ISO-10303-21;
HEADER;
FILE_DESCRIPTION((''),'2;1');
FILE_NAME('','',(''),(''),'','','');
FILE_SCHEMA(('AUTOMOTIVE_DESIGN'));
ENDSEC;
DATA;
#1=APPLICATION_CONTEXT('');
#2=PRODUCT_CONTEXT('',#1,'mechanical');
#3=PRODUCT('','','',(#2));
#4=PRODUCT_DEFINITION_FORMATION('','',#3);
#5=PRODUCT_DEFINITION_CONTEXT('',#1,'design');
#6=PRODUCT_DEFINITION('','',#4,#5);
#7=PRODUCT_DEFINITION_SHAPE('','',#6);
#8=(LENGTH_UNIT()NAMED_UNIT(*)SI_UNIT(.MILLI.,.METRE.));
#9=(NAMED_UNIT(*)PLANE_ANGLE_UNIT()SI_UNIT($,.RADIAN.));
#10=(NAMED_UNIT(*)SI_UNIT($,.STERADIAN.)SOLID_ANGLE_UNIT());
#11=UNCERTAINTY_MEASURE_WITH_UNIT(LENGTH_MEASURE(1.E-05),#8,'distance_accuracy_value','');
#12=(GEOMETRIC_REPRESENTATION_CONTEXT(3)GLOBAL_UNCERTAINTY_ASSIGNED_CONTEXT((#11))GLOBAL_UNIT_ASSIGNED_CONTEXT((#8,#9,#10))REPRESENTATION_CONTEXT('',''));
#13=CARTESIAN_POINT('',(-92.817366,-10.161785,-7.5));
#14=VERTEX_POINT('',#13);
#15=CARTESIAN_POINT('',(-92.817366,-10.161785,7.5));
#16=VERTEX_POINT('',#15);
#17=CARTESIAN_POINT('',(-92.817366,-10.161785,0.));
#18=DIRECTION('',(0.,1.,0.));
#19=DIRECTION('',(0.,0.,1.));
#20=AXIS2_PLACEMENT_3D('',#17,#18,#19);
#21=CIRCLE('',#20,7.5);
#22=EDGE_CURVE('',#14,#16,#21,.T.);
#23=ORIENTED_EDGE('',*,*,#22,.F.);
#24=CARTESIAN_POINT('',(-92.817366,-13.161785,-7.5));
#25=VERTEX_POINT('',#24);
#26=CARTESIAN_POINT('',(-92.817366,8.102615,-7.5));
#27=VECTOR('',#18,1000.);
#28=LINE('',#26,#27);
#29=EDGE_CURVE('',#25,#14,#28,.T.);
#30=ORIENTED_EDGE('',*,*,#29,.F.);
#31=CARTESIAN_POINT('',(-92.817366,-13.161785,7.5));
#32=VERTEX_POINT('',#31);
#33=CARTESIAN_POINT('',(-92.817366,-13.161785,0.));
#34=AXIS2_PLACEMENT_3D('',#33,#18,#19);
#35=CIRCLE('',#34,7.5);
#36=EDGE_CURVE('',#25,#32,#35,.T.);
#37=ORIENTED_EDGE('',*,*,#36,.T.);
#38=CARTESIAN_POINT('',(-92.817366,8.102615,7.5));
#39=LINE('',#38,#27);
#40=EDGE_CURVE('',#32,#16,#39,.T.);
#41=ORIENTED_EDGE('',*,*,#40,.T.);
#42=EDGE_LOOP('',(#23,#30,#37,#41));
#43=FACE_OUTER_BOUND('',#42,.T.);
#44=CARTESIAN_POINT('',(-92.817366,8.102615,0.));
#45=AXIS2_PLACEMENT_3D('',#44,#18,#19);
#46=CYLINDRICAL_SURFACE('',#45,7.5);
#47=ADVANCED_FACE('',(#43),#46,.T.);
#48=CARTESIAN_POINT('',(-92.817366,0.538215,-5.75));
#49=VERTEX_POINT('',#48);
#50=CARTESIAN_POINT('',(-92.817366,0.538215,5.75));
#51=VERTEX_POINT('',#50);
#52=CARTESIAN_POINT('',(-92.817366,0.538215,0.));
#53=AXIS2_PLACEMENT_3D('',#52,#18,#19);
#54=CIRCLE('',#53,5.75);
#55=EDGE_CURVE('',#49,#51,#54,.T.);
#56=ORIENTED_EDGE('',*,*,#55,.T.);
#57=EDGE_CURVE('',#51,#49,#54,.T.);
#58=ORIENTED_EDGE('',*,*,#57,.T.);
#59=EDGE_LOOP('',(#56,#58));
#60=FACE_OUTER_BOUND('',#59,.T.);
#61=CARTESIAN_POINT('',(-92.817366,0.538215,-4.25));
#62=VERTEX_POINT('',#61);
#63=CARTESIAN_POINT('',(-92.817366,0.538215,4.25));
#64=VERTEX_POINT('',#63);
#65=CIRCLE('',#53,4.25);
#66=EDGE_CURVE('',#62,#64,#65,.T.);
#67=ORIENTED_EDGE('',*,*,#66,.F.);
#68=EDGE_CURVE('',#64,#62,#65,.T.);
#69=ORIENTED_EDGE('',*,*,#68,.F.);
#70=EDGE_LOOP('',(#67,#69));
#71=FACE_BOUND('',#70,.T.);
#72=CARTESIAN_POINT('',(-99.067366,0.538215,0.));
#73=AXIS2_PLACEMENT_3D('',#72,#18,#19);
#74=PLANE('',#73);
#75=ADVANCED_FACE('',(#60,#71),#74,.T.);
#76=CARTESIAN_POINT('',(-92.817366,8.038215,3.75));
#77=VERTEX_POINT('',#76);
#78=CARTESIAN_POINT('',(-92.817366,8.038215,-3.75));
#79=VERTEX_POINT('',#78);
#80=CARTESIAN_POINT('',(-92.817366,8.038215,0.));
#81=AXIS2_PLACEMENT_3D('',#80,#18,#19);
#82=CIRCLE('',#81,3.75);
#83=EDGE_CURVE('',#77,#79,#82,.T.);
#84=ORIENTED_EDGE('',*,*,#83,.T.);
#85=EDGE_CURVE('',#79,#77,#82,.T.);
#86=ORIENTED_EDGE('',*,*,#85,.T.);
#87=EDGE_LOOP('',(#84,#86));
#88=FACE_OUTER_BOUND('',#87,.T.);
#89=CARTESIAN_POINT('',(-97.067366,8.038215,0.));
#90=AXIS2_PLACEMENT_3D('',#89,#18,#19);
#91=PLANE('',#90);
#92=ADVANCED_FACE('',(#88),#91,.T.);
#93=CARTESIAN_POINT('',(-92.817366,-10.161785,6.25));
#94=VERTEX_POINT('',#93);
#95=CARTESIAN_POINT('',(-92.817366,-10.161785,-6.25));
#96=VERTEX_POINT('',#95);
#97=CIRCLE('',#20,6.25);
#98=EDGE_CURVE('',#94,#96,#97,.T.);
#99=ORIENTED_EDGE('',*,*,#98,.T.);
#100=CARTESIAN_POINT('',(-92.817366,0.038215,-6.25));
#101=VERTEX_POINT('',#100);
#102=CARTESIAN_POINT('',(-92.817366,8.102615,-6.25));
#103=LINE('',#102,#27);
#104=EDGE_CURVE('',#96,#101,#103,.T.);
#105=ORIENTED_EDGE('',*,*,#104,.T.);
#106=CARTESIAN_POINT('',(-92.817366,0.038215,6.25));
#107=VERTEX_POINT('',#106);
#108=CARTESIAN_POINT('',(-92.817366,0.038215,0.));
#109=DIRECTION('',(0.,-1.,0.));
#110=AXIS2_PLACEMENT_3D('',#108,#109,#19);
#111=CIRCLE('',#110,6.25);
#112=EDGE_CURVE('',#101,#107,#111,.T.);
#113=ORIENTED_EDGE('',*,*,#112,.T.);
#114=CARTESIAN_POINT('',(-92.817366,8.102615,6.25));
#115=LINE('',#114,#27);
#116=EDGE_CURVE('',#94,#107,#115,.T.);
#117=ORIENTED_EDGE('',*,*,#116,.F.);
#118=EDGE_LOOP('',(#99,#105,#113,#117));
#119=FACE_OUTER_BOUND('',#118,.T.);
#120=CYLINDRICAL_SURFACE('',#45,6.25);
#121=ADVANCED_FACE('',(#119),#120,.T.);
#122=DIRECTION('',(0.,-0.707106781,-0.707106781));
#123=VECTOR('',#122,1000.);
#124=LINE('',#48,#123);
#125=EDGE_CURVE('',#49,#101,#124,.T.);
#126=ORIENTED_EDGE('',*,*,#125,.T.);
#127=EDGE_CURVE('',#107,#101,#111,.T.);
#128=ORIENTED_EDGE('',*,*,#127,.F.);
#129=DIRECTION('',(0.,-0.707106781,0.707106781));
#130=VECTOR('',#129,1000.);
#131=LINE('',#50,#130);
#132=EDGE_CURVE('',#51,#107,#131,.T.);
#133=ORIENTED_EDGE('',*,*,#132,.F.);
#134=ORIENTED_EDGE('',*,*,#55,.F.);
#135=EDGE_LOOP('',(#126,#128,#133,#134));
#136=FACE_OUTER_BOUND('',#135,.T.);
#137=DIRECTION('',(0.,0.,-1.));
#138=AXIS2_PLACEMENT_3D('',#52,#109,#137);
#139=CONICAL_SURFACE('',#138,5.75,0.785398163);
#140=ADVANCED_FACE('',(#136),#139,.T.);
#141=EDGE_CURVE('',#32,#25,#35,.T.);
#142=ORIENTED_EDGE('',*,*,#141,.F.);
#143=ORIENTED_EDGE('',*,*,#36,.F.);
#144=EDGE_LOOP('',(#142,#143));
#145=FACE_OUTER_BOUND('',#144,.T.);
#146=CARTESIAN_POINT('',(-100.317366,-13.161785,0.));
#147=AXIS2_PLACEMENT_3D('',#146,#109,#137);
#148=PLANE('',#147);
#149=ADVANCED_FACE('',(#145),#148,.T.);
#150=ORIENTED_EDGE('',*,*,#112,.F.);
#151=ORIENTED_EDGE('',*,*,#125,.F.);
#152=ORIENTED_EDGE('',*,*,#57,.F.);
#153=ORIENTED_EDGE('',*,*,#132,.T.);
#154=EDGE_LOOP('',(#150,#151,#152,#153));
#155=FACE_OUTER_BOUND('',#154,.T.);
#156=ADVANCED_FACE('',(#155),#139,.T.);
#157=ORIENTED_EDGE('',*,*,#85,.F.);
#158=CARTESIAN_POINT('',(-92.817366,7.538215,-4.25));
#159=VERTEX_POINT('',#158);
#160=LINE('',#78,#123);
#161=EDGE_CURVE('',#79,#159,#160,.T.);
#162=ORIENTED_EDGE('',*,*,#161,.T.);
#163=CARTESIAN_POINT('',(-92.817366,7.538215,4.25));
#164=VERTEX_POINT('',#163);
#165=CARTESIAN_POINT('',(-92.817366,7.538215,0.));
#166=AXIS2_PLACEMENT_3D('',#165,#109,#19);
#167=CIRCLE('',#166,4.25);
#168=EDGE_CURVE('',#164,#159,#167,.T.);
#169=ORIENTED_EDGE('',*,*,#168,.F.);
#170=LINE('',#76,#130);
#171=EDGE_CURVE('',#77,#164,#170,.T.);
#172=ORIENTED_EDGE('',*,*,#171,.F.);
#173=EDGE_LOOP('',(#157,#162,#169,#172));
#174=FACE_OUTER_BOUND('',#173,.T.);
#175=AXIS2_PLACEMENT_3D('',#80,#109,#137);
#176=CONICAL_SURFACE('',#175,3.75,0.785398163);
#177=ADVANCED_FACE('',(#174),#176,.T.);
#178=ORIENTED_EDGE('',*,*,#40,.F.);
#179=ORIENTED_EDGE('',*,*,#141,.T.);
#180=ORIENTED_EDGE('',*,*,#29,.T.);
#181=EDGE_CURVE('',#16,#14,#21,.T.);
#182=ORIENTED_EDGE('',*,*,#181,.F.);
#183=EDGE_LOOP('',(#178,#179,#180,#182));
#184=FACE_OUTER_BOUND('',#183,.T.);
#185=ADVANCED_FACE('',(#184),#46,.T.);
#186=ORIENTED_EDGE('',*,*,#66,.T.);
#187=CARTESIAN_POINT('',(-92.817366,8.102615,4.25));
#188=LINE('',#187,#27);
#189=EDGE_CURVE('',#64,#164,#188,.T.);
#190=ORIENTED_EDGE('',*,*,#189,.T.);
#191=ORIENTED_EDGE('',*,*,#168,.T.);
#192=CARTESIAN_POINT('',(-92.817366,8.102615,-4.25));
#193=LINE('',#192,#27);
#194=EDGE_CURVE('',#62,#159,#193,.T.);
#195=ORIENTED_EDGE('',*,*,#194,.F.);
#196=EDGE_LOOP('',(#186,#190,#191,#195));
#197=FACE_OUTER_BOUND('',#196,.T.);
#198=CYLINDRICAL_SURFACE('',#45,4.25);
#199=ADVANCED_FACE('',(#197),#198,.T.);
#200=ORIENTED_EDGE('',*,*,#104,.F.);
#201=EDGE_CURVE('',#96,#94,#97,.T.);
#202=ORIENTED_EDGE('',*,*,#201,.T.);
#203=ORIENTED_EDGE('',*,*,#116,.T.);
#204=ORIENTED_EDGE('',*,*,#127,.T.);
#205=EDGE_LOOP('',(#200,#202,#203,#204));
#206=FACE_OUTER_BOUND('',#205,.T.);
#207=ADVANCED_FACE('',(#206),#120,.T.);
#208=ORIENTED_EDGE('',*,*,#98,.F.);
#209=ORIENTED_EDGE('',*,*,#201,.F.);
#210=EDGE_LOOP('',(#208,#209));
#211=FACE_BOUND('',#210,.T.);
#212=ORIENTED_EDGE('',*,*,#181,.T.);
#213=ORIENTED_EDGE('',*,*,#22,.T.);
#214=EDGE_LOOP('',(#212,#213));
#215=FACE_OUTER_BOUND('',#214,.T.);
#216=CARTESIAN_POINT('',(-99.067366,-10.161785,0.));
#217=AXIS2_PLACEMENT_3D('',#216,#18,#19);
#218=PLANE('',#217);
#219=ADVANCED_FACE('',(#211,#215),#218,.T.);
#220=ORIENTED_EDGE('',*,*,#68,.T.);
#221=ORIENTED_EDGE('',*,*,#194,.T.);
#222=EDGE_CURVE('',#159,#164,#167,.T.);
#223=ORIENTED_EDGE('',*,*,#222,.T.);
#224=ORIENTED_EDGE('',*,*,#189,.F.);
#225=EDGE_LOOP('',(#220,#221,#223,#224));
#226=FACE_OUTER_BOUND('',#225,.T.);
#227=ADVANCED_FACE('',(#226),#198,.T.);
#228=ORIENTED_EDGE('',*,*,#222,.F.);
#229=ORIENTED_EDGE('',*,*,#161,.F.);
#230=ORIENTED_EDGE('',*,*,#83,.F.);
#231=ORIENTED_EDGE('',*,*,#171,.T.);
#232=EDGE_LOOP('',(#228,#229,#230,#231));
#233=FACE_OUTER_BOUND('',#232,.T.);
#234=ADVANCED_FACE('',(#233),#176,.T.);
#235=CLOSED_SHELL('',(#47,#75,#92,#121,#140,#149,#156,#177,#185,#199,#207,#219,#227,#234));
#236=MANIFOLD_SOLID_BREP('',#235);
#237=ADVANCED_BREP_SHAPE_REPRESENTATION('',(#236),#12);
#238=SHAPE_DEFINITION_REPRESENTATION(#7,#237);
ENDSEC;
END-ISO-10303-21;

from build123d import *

# Parameters (mm, degrees)
CHAMFER1_SIZE = 0.5


with BuildPart() as part:
    # Sketch1 → Revolve1 (revolve)
    with BuildSketch(Plane.XY, mode=Mode.PRIVATE) as revolve1_sk:
        Polygon((-99.067365632, -10.161784701), (-100.317365632, -10.161784701), (-100.317365632, -13.161784701), (-92.817365632, -13.161784701), (-92.817365632, 8.038215299), (-97.067365632, 8.038215299), (-97.067365632, 0.538215299), (-99.067365632, 0.538215299), align=None)
    revolve(revolve1_sk.sketch.rotate(Axis((-92.817365632, 8.102615299, 0), (0, -1, 0)), 270), axis=Axis((-92.817365632, 8.102615299, 0), (0, -1, 0)))

    # Chamfer1
    chamfer1_edges = [part.edges().sort_by_distance(p)[0] for p in [
        (-92.817365632, 0.538215299, -6.25),
        (-92.817365632, 8.038215299, -4.25),
    ]]
    chamfer(chamfer1_edges, length=CHAMFER1_SIZE)


solid = part.part
